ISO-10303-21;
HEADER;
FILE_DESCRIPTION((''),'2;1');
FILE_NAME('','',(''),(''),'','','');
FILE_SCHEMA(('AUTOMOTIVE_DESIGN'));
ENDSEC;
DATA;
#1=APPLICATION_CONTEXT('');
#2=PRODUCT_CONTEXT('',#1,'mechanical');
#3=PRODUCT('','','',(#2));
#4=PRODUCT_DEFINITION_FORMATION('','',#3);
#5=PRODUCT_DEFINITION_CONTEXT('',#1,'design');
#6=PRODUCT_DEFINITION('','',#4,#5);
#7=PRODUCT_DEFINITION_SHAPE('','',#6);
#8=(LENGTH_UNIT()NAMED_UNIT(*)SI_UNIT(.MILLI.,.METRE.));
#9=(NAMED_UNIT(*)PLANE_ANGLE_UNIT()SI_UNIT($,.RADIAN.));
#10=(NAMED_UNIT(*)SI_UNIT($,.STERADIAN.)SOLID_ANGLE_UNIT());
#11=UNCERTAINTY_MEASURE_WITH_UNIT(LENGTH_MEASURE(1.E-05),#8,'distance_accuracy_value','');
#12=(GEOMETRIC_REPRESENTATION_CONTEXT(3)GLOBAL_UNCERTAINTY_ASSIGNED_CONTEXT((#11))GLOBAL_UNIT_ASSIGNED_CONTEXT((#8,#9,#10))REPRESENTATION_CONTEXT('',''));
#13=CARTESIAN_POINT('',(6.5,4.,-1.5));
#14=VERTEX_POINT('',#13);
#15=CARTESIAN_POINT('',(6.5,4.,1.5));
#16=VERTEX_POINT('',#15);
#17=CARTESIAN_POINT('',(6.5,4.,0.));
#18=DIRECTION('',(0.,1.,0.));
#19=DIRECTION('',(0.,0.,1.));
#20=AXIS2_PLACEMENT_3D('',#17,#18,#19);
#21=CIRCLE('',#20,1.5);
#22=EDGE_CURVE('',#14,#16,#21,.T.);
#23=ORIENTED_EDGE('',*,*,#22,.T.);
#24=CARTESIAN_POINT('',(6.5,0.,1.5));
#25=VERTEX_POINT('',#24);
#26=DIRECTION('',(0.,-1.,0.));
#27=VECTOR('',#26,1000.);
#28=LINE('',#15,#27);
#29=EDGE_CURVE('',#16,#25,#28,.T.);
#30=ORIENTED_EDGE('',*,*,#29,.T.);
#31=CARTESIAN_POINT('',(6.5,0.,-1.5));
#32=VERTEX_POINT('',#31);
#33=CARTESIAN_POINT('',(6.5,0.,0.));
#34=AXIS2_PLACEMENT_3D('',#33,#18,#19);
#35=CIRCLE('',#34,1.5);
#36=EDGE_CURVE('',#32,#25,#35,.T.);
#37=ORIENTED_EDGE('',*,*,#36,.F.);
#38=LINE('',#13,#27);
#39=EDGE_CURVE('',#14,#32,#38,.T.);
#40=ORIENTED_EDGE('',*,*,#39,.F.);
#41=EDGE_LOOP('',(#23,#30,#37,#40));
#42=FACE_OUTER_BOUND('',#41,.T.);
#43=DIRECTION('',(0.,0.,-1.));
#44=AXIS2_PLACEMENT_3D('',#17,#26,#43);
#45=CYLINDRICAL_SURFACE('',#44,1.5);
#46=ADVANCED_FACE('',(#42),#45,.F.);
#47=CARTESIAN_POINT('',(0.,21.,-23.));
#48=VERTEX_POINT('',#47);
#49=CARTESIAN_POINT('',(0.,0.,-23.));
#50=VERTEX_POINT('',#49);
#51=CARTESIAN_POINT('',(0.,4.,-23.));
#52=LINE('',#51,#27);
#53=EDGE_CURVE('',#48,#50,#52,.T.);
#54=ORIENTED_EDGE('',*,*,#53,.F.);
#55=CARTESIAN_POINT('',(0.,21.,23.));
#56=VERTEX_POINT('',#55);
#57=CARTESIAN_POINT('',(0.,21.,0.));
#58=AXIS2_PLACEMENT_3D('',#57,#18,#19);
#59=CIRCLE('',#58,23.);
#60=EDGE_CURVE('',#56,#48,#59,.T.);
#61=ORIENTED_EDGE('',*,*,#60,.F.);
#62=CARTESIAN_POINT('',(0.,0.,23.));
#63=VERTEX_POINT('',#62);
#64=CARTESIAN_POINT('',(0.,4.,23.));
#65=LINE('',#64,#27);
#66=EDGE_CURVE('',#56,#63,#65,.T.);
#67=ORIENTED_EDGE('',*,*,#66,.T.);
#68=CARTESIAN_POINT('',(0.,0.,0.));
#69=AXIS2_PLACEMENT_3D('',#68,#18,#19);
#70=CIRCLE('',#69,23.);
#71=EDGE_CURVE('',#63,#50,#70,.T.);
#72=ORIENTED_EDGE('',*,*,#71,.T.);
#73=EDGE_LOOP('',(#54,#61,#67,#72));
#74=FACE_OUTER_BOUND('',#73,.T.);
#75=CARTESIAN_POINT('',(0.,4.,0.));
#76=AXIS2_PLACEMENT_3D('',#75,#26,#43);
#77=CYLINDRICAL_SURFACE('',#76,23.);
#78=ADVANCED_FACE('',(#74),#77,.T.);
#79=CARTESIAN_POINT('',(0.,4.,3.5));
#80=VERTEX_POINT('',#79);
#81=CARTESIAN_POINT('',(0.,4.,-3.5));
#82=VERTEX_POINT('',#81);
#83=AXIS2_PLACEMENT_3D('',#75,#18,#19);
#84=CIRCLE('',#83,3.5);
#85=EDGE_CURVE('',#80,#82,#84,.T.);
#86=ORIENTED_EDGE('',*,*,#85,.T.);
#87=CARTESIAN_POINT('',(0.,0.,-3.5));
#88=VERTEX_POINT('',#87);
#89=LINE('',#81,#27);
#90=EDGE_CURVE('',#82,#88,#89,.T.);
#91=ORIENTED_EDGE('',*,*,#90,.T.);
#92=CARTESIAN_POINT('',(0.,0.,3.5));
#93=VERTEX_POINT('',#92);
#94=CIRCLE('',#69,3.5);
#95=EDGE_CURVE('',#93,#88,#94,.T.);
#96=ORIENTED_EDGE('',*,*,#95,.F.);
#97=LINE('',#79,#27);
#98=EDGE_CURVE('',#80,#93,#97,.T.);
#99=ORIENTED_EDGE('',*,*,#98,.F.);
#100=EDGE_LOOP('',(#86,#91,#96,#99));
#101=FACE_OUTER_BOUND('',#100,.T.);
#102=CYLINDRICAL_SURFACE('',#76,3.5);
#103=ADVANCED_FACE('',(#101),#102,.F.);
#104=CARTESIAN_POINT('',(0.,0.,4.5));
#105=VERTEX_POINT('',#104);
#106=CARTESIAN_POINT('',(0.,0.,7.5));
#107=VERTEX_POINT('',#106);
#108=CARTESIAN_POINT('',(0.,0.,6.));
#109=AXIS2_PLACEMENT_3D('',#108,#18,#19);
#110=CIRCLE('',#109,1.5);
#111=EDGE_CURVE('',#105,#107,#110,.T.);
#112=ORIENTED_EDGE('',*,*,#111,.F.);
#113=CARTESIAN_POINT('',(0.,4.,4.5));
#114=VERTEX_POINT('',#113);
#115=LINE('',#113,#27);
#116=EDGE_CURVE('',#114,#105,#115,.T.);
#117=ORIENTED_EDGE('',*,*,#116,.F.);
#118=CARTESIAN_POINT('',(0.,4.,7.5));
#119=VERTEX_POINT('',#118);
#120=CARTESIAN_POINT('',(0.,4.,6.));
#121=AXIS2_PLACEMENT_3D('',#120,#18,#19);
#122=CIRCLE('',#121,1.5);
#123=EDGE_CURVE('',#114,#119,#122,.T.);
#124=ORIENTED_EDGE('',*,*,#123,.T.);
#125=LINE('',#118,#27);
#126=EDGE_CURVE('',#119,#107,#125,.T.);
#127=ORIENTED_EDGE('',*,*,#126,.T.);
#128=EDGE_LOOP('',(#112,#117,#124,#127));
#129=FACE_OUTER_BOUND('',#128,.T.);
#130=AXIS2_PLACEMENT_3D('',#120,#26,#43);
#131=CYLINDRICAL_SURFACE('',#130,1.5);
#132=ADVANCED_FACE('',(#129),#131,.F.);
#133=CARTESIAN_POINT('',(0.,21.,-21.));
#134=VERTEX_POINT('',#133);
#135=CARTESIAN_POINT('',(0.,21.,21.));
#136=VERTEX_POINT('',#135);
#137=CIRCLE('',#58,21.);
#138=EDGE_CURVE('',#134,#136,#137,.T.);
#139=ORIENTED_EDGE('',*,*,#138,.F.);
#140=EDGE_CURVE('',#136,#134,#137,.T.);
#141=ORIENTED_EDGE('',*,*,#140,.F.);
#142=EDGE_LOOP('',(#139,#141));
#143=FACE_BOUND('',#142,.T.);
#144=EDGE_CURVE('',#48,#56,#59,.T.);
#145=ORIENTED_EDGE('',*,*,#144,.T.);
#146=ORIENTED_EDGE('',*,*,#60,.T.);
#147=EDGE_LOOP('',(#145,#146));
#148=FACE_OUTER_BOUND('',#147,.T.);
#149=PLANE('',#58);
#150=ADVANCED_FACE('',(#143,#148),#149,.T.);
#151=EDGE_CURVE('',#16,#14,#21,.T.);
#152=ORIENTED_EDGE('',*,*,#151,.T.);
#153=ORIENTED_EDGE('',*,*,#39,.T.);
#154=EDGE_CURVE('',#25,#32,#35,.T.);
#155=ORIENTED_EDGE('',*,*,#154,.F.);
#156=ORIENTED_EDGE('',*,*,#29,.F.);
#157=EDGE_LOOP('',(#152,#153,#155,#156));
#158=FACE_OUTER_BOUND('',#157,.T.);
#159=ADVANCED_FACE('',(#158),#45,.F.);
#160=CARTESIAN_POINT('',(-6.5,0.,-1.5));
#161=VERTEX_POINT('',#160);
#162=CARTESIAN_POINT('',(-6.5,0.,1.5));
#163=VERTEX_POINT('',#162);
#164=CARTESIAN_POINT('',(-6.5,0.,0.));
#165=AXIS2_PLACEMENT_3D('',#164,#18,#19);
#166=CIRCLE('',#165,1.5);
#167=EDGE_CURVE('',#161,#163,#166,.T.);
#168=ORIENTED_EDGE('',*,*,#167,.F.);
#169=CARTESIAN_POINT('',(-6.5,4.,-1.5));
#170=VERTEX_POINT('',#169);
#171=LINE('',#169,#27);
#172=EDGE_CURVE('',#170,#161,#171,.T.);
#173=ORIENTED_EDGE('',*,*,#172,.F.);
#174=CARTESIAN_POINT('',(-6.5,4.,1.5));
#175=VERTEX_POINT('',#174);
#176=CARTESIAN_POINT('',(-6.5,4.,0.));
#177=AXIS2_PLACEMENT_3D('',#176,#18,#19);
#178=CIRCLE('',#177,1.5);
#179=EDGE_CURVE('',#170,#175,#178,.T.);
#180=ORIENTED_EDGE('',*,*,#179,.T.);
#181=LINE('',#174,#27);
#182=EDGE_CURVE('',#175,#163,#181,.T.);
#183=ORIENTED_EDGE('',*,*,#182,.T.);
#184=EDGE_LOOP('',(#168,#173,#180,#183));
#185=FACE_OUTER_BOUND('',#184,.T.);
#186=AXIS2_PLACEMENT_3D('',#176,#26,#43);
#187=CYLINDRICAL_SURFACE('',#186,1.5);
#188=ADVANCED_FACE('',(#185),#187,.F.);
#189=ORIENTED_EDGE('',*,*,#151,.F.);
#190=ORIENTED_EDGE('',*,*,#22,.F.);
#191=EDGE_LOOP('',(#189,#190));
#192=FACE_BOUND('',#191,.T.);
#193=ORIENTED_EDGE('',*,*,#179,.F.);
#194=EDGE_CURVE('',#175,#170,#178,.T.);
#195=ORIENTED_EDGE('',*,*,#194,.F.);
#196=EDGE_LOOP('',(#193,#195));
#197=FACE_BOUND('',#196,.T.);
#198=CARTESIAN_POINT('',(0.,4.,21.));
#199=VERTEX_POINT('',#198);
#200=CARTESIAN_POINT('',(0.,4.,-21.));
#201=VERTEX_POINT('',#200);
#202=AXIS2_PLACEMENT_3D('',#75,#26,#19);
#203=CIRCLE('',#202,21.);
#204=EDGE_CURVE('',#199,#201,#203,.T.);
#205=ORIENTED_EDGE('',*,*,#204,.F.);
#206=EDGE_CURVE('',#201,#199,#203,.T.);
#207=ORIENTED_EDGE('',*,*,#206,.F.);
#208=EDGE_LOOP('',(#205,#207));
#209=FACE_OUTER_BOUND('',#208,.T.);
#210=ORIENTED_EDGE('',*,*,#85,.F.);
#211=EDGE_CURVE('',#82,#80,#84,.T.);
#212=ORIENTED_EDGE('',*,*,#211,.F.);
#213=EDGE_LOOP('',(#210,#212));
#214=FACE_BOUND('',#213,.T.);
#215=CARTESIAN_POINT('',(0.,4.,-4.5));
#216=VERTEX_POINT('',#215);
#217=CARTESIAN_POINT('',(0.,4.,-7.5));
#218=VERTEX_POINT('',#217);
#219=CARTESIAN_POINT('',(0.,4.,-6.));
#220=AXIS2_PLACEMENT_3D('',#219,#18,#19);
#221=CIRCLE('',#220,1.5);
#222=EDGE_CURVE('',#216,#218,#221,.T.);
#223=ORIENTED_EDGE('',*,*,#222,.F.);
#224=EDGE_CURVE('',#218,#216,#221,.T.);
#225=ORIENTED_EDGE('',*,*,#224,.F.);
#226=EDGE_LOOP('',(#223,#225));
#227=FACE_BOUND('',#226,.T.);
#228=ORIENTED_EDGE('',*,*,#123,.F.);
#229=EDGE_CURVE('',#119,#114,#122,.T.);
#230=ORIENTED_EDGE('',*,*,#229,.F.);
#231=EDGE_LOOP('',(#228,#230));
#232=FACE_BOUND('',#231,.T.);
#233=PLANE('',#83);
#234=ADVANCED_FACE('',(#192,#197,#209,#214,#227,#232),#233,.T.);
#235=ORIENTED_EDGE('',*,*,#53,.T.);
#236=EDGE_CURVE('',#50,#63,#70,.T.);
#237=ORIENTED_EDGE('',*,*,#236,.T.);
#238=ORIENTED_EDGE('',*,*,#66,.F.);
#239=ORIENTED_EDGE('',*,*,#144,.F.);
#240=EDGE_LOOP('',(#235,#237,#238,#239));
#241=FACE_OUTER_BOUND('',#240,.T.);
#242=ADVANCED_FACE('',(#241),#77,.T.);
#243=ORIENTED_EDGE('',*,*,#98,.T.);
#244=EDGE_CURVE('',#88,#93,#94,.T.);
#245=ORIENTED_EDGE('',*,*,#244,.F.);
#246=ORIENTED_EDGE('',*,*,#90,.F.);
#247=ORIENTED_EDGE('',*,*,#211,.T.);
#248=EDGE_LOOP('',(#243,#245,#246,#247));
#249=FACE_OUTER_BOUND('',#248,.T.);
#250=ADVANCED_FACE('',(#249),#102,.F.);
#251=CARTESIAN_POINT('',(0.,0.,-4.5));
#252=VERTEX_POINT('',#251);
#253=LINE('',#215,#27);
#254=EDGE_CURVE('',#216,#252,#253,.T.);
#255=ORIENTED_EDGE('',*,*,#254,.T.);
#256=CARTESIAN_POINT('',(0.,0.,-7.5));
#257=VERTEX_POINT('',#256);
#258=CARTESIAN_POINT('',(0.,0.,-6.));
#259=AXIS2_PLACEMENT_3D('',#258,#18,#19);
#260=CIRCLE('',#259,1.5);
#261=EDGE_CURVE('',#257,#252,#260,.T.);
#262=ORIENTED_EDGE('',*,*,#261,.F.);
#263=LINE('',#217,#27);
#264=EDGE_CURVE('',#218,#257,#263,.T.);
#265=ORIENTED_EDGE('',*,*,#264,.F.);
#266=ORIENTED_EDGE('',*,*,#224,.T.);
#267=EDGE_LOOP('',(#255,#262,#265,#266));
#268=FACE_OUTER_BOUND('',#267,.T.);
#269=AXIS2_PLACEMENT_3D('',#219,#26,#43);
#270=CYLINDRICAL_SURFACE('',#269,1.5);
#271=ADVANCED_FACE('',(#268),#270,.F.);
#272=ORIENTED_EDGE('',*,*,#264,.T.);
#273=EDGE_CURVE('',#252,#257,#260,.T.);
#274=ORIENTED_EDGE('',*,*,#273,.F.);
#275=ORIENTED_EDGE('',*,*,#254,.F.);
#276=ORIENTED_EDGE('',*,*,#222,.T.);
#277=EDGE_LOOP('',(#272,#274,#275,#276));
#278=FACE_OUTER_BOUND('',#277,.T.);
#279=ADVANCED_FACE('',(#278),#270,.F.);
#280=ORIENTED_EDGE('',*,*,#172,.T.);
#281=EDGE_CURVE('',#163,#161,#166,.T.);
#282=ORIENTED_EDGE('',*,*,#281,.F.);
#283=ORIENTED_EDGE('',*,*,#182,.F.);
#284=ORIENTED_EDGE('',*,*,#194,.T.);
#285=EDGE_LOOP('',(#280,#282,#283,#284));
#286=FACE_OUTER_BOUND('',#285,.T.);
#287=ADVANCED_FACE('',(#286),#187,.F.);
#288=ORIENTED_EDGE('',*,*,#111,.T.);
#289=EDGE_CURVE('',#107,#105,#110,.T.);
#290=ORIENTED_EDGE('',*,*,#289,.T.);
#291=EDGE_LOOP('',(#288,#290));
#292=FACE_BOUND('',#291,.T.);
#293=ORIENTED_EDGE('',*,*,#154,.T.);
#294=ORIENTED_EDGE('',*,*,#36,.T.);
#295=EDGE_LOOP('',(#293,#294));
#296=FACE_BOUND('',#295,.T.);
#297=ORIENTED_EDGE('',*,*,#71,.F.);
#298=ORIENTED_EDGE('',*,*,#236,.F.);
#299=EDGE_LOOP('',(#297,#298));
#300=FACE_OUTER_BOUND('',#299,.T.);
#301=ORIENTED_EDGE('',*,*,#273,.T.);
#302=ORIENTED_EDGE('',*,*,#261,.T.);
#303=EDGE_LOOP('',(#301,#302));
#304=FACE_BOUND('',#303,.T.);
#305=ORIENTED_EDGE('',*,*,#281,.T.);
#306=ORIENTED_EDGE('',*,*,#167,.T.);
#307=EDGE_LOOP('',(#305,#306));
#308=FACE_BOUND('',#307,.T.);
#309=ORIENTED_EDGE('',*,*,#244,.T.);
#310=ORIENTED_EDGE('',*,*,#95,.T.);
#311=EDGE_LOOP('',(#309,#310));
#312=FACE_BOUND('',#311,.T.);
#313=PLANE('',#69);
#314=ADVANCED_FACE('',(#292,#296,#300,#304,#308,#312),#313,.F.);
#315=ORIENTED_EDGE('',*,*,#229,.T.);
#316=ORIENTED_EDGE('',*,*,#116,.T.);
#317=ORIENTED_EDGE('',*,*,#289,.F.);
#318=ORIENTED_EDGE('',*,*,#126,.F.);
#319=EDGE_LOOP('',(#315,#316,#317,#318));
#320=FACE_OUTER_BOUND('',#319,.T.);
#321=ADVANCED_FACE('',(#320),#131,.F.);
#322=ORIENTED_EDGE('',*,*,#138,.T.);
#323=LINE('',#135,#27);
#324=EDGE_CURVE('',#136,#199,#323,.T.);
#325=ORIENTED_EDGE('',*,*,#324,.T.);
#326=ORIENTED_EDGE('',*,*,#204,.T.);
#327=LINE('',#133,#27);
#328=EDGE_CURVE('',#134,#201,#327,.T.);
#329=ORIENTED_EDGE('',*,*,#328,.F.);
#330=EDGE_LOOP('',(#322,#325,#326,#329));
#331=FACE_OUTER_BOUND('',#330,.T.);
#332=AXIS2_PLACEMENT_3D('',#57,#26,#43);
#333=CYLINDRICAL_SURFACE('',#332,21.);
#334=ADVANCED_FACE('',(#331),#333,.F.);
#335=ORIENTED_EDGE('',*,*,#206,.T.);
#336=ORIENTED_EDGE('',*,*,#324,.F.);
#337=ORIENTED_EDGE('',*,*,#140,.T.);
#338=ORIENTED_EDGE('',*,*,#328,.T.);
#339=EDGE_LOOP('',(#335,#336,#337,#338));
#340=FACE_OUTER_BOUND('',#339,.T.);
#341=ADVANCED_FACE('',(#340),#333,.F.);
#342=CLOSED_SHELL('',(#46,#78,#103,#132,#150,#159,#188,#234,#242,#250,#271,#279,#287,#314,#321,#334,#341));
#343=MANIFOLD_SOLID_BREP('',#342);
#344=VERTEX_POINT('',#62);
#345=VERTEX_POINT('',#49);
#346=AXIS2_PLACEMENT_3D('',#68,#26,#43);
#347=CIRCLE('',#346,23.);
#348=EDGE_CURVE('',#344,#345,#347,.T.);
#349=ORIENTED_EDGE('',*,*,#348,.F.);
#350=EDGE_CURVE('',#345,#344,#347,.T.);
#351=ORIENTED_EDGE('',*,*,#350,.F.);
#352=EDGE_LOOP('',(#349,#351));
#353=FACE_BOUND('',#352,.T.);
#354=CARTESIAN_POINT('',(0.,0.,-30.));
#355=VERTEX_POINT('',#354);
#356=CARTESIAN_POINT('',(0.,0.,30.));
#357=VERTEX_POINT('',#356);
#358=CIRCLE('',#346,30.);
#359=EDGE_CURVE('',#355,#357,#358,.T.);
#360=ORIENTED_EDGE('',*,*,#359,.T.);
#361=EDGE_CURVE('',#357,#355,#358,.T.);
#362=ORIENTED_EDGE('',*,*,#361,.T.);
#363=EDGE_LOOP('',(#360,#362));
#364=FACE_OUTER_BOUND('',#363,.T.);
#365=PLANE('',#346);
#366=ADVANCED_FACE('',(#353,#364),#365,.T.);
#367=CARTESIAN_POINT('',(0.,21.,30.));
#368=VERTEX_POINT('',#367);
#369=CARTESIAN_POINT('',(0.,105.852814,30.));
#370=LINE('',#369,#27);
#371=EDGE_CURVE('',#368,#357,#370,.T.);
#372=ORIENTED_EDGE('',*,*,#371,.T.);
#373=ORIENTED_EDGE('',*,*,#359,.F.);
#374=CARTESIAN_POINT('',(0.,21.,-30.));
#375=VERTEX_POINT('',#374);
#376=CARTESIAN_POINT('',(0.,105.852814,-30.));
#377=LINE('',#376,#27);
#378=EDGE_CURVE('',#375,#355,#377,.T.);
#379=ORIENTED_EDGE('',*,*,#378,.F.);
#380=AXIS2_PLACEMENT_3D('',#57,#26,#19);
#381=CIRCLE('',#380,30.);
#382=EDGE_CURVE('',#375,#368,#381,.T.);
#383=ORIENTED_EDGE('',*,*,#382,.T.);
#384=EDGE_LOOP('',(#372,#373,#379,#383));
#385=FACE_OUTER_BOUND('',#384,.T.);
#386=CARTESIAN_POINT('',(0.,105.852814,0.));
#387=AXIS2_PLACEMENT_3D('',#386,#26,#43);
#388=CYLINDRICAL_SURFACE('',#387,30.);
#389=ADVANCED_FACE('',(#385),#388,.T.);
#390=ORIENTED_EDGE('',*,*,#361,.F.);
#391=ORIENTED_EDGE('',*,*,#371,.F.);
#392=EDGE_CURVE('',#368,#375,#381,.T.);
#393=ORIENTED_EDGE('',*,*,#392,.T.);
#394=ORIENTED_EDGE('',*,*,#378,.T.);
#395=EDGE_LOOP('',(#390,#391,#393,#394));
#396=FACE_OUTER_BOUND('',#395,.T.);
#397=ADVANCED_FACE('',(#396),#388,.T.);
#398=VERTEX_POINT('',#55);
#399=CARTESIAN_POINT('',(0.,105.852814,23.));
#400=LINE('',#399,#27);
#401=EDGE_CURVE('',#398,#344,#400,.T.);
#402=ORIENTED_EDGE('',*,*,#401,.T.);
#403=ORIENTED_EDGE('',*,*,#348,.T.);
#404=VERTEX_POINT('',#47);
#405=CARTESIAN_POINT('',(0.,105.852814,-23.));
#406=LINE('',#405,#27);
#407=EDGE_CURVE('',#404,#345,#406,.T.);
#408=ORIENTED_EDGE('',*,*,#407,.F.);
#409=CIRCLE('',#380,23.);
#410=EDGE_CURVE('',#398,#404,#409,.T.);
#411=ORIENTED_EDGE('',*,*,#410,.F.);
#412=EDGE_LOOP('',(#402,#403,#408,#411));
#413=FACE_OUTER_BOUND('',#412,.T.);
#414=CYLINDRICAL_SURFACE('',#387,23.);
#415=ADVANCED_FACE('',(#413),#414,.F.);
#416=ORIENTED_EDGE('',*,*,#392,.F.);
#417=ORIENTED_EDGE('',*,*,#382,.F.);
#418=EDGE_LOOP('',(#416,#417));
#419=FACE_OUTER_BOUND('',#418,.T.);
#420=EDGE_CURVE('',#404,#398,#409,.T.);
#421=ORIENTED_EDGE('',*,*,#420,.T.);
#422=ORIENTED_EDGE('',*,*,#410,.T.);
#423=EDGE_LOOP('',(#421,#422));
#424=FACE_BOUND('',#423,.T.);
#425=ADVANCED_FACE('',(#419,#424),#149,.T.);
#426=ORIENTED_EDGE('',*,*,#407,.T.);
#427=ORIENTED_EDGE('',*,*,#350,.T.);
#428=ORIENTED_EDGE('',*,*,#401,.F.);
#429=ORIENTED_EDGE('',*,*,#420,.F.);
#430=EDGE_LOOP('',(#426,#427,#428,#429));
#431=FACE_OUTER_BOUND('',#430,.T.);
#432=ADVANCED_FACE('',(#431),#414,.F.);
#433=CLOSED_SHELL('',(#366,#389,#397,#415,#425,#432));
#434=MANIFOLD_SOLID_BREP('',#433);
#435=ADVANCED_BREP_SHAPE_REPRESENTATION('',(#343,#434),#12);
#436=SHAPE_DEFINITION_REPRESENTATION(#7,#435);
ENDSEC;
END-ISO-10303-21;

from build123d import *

# Parameters (mm, degrees)
SKETCH_1_R      = 23
SKETCH_1_R_2    = 1.5
SKETCH_1_R_3    = 3.5
EXTRUDE_1_DEPTH = 4
SKETCH_2_R      = 23
SKETCH_2_R_2    = 21
EXTRUDE_2_DEPTH = 17
SKETCH_3_R      = 30
SKETCH_3_R_2    = 23
EXTRUDE_3_DEPTH = 21


with BuildPart() as part:
    # 草图1 → 凸台-拉伸1 (new body)
    with BuildSketch(Plane(origin=(0, 0, 0), x_dir=(1, 0, 0), z_dir=(0, 1, 0))):
        with Locations(Location((0, 0, 0), (0, 0, 270))):
            Circle(SKETCH_1_R)
        with Locations(Location((6.5, 0, 0), (0, 0, 270))):
            Circle(SKETCH_1_R_2, mode=Mode.SUBTRACT)
        with Locations(Location((-6.5, 0, 0), (0, 0, 270))):
            Circle(SKETCH_1_R_2, mode=Mode.SUBTRACT)
        with Locations(Location((0, -6, 0), (0, 0, 270))):
            Circle(SKETCH_1_R_2, mode=Mode.SUBTRACT)
        with Locations(Location((0, 6, 0), (0, 0, 270))):
            Circle(SKETCH_1_R_2, mode=Mode.SUBTRACT)
        with Locations(Location((0, 0, 0), (0, 0, 270))):
            Circle(SKETCH_1_R_3, mode=Mode.SUBTRACT)
    extrude(amount=EXTRUDE_1_DEPTH)

    # 草图2 → 凸台-拉伸2 (add)
    with BuildSketch(Plane(origin=(0, 4, 0), x_dir=(1, 0, 0), z_dir=(0, 1, 0))):
        with Locations(Location((0, 0, 0), (0, 0, 270))):
            Circle(SKETCH_2_R)
        with Locations(Location((0, 0, 0), (0, 0, 270))):
            Circle(SKETCH_2_R_2, mode=Mode.SUBTRACT)
    extrude(amount=EXTRUDE_2_DEPTH)


with BuildPart() as body_2:
    # 草图3 → 凸台-拉伸3 (new body)
    with BuildSketch(Plane.XZ):
        with Locations(Location((0, 0, 0), (0, 0, 270))):
            Circle(SKETCH_3_R)
        with Locations(Location((0, 0, 0), (0, 0, 270))):
            Circle(SKETCH_3_R_2, mode=Mode.SUBTRACT)
    extrude(amount=-EXTRUDE_3_DEPTH)


solid = Compound([part.part, body_2.part])
